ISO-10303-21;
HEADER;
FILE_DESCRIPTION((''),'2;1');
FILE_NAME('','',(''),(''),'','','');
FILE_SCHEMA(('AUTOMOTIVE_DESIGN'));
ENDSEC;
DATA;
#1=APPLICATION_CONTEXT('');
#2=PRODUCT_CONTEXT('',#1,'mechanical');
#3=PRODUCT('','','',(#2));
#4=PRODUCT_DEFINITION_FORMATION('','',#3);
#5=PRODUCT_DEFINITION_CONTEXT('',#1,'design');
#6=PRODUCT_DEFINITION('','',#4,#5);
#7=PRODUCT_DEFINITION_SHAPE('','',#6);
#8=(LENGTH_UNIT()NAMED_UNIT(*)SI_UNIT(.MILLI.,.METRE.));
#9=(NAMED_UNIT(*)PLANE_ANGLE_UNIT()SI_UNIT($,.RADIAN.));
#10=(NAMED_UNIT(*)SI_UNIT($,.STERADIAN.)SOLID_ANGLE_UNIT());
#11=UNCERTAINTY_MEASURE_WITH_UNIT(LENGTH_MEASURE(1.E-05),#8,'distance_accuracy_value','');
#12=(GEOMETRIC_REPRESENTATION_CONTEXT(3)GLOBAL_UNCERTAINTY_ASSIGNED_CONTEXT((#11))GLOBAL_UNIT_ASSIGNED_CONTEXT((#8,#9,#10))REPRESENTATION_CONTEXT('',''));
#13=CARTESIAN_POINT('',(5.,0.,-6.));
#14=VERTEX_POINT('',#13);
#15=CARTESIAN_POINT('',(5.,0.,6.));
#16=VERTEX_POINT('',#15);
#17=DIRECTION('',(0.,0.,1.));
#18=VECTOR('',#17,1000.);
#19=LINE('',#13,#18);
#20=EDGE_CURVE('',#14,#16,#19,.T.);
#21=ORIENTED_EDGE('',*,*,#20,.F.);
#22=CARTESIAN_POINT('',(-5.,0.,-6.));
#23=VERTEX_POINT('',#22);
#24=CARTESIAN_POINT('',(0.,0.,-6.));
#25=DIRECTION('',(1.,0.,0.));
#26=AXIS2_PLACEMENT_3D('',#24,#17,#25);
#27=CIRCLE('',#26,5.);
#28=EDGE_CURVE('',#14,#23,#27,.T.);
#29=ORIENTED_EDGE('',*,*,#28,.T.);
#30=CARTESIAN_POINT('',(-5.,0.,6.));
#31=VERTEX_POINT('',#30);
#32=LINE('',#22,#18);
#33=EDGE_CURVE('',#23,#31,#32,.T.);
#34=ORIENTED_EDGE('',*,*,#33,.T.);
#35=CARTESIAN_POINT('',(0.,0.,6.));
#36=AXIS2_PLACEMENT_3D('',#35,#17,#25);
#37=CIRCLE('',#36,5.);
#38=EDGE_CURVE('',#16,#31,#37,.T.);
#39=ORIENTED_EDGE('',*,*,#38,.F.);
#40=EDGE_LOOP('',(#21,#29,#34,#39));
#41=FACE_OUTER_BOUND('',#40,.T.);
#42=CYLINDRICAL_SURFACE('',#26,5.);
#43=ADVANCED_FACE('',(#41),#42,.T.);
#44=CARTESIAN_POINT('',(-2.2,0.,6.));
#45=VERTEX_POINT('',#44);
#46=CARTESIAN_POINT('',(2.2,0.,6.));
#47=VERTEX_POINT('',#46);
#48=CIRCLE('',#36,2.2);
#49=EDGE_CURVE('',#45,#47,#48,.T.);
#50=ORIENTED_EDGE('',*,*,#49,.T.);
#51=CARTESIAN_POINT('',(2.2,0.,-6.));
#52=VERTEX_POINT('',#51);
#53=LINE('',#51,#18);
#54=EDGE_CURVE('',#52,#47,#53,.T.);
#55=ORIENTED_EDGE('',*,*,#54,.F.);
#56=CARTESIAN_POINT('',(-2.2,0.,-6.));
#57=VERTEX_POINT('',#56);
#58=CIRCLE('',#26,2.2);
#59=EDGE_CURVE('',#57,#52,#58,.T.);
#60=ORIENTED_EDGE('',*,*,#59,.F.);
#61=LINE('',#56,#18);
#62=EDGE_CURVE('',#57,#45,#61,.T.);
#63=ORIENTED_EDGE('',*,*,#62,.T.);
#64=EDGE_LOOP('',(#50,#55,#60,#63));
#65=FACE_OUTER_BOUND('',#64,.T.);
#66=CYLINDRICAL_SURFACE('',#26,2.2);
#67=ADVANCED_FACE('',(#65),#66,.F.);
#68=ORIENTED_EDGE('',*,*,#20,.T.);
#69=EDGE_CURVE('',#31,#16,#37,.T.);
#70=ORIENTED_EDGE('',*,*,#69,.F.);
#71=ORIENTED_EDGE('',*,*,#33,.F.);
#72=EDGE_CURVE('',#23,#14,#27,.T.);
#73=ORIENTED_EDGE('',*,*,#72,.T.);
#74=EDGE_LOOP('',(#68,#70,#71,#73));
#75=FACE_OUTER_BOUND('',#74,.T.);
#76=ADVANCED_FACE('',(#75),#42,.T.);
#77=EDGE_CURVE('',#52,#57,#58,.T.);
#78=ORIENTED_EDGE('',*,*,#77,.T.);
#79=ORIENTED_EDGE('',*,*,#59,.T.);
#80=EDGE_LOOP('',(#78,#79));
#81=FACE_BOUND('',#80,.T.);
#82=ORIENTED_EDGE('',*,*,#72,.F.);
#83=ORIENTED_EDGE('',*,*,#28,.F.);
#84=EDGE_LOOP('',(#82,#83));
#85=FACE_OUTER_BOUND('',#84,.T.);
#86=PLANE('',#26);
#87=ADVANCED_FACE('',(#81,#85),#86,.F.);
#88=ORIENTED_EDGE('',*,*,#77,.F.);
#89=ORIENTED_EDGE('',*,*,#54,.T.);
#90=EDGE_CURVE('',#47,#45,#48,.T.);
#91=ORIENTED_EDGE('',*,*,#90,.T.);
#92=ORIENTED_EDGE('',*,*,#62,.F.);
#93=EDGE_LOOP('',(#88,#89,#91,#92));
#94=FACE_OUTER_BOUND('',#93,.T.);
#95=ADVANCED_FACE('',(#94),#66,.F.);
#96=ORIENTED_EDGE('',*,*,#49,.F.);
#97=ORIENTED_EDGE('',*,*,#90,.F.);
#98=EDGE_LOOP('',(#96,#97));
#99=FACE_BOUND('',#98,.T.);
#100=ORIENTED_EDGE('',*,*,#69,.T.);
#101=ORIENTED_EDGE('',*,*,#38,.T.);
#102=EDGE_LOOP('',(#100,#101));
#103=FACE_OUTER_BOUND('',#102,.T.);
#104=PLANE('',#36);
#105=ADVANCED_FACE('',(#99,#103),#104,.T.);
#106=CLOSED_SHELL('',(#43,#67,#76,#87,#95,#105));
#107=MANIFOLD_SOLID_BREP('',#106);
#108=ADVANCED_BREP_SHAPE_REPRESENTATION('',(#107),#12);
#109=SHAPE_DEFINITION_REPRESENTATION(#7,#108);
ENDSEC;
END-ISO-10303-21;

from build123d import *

# Parameters (mm, degrees)
SKETCH_1_R      = 5
SKETCH_1_R_2    = 2.2
EXTRUDE_1_DEPTH = 6


with BuildPart() as part:
    # 草图1 → 凸台-拉伸1 (new, symmetric)
    with BuildSketch(Plane.XY):
        Circle(SKETCH_1_R)
        Circle(SKETCH_1_R_2, mode=Mode.SUBTRACT)
    extrude(amount=EXTRUDE_1_DEPTH, both=True)


solid = part.part
